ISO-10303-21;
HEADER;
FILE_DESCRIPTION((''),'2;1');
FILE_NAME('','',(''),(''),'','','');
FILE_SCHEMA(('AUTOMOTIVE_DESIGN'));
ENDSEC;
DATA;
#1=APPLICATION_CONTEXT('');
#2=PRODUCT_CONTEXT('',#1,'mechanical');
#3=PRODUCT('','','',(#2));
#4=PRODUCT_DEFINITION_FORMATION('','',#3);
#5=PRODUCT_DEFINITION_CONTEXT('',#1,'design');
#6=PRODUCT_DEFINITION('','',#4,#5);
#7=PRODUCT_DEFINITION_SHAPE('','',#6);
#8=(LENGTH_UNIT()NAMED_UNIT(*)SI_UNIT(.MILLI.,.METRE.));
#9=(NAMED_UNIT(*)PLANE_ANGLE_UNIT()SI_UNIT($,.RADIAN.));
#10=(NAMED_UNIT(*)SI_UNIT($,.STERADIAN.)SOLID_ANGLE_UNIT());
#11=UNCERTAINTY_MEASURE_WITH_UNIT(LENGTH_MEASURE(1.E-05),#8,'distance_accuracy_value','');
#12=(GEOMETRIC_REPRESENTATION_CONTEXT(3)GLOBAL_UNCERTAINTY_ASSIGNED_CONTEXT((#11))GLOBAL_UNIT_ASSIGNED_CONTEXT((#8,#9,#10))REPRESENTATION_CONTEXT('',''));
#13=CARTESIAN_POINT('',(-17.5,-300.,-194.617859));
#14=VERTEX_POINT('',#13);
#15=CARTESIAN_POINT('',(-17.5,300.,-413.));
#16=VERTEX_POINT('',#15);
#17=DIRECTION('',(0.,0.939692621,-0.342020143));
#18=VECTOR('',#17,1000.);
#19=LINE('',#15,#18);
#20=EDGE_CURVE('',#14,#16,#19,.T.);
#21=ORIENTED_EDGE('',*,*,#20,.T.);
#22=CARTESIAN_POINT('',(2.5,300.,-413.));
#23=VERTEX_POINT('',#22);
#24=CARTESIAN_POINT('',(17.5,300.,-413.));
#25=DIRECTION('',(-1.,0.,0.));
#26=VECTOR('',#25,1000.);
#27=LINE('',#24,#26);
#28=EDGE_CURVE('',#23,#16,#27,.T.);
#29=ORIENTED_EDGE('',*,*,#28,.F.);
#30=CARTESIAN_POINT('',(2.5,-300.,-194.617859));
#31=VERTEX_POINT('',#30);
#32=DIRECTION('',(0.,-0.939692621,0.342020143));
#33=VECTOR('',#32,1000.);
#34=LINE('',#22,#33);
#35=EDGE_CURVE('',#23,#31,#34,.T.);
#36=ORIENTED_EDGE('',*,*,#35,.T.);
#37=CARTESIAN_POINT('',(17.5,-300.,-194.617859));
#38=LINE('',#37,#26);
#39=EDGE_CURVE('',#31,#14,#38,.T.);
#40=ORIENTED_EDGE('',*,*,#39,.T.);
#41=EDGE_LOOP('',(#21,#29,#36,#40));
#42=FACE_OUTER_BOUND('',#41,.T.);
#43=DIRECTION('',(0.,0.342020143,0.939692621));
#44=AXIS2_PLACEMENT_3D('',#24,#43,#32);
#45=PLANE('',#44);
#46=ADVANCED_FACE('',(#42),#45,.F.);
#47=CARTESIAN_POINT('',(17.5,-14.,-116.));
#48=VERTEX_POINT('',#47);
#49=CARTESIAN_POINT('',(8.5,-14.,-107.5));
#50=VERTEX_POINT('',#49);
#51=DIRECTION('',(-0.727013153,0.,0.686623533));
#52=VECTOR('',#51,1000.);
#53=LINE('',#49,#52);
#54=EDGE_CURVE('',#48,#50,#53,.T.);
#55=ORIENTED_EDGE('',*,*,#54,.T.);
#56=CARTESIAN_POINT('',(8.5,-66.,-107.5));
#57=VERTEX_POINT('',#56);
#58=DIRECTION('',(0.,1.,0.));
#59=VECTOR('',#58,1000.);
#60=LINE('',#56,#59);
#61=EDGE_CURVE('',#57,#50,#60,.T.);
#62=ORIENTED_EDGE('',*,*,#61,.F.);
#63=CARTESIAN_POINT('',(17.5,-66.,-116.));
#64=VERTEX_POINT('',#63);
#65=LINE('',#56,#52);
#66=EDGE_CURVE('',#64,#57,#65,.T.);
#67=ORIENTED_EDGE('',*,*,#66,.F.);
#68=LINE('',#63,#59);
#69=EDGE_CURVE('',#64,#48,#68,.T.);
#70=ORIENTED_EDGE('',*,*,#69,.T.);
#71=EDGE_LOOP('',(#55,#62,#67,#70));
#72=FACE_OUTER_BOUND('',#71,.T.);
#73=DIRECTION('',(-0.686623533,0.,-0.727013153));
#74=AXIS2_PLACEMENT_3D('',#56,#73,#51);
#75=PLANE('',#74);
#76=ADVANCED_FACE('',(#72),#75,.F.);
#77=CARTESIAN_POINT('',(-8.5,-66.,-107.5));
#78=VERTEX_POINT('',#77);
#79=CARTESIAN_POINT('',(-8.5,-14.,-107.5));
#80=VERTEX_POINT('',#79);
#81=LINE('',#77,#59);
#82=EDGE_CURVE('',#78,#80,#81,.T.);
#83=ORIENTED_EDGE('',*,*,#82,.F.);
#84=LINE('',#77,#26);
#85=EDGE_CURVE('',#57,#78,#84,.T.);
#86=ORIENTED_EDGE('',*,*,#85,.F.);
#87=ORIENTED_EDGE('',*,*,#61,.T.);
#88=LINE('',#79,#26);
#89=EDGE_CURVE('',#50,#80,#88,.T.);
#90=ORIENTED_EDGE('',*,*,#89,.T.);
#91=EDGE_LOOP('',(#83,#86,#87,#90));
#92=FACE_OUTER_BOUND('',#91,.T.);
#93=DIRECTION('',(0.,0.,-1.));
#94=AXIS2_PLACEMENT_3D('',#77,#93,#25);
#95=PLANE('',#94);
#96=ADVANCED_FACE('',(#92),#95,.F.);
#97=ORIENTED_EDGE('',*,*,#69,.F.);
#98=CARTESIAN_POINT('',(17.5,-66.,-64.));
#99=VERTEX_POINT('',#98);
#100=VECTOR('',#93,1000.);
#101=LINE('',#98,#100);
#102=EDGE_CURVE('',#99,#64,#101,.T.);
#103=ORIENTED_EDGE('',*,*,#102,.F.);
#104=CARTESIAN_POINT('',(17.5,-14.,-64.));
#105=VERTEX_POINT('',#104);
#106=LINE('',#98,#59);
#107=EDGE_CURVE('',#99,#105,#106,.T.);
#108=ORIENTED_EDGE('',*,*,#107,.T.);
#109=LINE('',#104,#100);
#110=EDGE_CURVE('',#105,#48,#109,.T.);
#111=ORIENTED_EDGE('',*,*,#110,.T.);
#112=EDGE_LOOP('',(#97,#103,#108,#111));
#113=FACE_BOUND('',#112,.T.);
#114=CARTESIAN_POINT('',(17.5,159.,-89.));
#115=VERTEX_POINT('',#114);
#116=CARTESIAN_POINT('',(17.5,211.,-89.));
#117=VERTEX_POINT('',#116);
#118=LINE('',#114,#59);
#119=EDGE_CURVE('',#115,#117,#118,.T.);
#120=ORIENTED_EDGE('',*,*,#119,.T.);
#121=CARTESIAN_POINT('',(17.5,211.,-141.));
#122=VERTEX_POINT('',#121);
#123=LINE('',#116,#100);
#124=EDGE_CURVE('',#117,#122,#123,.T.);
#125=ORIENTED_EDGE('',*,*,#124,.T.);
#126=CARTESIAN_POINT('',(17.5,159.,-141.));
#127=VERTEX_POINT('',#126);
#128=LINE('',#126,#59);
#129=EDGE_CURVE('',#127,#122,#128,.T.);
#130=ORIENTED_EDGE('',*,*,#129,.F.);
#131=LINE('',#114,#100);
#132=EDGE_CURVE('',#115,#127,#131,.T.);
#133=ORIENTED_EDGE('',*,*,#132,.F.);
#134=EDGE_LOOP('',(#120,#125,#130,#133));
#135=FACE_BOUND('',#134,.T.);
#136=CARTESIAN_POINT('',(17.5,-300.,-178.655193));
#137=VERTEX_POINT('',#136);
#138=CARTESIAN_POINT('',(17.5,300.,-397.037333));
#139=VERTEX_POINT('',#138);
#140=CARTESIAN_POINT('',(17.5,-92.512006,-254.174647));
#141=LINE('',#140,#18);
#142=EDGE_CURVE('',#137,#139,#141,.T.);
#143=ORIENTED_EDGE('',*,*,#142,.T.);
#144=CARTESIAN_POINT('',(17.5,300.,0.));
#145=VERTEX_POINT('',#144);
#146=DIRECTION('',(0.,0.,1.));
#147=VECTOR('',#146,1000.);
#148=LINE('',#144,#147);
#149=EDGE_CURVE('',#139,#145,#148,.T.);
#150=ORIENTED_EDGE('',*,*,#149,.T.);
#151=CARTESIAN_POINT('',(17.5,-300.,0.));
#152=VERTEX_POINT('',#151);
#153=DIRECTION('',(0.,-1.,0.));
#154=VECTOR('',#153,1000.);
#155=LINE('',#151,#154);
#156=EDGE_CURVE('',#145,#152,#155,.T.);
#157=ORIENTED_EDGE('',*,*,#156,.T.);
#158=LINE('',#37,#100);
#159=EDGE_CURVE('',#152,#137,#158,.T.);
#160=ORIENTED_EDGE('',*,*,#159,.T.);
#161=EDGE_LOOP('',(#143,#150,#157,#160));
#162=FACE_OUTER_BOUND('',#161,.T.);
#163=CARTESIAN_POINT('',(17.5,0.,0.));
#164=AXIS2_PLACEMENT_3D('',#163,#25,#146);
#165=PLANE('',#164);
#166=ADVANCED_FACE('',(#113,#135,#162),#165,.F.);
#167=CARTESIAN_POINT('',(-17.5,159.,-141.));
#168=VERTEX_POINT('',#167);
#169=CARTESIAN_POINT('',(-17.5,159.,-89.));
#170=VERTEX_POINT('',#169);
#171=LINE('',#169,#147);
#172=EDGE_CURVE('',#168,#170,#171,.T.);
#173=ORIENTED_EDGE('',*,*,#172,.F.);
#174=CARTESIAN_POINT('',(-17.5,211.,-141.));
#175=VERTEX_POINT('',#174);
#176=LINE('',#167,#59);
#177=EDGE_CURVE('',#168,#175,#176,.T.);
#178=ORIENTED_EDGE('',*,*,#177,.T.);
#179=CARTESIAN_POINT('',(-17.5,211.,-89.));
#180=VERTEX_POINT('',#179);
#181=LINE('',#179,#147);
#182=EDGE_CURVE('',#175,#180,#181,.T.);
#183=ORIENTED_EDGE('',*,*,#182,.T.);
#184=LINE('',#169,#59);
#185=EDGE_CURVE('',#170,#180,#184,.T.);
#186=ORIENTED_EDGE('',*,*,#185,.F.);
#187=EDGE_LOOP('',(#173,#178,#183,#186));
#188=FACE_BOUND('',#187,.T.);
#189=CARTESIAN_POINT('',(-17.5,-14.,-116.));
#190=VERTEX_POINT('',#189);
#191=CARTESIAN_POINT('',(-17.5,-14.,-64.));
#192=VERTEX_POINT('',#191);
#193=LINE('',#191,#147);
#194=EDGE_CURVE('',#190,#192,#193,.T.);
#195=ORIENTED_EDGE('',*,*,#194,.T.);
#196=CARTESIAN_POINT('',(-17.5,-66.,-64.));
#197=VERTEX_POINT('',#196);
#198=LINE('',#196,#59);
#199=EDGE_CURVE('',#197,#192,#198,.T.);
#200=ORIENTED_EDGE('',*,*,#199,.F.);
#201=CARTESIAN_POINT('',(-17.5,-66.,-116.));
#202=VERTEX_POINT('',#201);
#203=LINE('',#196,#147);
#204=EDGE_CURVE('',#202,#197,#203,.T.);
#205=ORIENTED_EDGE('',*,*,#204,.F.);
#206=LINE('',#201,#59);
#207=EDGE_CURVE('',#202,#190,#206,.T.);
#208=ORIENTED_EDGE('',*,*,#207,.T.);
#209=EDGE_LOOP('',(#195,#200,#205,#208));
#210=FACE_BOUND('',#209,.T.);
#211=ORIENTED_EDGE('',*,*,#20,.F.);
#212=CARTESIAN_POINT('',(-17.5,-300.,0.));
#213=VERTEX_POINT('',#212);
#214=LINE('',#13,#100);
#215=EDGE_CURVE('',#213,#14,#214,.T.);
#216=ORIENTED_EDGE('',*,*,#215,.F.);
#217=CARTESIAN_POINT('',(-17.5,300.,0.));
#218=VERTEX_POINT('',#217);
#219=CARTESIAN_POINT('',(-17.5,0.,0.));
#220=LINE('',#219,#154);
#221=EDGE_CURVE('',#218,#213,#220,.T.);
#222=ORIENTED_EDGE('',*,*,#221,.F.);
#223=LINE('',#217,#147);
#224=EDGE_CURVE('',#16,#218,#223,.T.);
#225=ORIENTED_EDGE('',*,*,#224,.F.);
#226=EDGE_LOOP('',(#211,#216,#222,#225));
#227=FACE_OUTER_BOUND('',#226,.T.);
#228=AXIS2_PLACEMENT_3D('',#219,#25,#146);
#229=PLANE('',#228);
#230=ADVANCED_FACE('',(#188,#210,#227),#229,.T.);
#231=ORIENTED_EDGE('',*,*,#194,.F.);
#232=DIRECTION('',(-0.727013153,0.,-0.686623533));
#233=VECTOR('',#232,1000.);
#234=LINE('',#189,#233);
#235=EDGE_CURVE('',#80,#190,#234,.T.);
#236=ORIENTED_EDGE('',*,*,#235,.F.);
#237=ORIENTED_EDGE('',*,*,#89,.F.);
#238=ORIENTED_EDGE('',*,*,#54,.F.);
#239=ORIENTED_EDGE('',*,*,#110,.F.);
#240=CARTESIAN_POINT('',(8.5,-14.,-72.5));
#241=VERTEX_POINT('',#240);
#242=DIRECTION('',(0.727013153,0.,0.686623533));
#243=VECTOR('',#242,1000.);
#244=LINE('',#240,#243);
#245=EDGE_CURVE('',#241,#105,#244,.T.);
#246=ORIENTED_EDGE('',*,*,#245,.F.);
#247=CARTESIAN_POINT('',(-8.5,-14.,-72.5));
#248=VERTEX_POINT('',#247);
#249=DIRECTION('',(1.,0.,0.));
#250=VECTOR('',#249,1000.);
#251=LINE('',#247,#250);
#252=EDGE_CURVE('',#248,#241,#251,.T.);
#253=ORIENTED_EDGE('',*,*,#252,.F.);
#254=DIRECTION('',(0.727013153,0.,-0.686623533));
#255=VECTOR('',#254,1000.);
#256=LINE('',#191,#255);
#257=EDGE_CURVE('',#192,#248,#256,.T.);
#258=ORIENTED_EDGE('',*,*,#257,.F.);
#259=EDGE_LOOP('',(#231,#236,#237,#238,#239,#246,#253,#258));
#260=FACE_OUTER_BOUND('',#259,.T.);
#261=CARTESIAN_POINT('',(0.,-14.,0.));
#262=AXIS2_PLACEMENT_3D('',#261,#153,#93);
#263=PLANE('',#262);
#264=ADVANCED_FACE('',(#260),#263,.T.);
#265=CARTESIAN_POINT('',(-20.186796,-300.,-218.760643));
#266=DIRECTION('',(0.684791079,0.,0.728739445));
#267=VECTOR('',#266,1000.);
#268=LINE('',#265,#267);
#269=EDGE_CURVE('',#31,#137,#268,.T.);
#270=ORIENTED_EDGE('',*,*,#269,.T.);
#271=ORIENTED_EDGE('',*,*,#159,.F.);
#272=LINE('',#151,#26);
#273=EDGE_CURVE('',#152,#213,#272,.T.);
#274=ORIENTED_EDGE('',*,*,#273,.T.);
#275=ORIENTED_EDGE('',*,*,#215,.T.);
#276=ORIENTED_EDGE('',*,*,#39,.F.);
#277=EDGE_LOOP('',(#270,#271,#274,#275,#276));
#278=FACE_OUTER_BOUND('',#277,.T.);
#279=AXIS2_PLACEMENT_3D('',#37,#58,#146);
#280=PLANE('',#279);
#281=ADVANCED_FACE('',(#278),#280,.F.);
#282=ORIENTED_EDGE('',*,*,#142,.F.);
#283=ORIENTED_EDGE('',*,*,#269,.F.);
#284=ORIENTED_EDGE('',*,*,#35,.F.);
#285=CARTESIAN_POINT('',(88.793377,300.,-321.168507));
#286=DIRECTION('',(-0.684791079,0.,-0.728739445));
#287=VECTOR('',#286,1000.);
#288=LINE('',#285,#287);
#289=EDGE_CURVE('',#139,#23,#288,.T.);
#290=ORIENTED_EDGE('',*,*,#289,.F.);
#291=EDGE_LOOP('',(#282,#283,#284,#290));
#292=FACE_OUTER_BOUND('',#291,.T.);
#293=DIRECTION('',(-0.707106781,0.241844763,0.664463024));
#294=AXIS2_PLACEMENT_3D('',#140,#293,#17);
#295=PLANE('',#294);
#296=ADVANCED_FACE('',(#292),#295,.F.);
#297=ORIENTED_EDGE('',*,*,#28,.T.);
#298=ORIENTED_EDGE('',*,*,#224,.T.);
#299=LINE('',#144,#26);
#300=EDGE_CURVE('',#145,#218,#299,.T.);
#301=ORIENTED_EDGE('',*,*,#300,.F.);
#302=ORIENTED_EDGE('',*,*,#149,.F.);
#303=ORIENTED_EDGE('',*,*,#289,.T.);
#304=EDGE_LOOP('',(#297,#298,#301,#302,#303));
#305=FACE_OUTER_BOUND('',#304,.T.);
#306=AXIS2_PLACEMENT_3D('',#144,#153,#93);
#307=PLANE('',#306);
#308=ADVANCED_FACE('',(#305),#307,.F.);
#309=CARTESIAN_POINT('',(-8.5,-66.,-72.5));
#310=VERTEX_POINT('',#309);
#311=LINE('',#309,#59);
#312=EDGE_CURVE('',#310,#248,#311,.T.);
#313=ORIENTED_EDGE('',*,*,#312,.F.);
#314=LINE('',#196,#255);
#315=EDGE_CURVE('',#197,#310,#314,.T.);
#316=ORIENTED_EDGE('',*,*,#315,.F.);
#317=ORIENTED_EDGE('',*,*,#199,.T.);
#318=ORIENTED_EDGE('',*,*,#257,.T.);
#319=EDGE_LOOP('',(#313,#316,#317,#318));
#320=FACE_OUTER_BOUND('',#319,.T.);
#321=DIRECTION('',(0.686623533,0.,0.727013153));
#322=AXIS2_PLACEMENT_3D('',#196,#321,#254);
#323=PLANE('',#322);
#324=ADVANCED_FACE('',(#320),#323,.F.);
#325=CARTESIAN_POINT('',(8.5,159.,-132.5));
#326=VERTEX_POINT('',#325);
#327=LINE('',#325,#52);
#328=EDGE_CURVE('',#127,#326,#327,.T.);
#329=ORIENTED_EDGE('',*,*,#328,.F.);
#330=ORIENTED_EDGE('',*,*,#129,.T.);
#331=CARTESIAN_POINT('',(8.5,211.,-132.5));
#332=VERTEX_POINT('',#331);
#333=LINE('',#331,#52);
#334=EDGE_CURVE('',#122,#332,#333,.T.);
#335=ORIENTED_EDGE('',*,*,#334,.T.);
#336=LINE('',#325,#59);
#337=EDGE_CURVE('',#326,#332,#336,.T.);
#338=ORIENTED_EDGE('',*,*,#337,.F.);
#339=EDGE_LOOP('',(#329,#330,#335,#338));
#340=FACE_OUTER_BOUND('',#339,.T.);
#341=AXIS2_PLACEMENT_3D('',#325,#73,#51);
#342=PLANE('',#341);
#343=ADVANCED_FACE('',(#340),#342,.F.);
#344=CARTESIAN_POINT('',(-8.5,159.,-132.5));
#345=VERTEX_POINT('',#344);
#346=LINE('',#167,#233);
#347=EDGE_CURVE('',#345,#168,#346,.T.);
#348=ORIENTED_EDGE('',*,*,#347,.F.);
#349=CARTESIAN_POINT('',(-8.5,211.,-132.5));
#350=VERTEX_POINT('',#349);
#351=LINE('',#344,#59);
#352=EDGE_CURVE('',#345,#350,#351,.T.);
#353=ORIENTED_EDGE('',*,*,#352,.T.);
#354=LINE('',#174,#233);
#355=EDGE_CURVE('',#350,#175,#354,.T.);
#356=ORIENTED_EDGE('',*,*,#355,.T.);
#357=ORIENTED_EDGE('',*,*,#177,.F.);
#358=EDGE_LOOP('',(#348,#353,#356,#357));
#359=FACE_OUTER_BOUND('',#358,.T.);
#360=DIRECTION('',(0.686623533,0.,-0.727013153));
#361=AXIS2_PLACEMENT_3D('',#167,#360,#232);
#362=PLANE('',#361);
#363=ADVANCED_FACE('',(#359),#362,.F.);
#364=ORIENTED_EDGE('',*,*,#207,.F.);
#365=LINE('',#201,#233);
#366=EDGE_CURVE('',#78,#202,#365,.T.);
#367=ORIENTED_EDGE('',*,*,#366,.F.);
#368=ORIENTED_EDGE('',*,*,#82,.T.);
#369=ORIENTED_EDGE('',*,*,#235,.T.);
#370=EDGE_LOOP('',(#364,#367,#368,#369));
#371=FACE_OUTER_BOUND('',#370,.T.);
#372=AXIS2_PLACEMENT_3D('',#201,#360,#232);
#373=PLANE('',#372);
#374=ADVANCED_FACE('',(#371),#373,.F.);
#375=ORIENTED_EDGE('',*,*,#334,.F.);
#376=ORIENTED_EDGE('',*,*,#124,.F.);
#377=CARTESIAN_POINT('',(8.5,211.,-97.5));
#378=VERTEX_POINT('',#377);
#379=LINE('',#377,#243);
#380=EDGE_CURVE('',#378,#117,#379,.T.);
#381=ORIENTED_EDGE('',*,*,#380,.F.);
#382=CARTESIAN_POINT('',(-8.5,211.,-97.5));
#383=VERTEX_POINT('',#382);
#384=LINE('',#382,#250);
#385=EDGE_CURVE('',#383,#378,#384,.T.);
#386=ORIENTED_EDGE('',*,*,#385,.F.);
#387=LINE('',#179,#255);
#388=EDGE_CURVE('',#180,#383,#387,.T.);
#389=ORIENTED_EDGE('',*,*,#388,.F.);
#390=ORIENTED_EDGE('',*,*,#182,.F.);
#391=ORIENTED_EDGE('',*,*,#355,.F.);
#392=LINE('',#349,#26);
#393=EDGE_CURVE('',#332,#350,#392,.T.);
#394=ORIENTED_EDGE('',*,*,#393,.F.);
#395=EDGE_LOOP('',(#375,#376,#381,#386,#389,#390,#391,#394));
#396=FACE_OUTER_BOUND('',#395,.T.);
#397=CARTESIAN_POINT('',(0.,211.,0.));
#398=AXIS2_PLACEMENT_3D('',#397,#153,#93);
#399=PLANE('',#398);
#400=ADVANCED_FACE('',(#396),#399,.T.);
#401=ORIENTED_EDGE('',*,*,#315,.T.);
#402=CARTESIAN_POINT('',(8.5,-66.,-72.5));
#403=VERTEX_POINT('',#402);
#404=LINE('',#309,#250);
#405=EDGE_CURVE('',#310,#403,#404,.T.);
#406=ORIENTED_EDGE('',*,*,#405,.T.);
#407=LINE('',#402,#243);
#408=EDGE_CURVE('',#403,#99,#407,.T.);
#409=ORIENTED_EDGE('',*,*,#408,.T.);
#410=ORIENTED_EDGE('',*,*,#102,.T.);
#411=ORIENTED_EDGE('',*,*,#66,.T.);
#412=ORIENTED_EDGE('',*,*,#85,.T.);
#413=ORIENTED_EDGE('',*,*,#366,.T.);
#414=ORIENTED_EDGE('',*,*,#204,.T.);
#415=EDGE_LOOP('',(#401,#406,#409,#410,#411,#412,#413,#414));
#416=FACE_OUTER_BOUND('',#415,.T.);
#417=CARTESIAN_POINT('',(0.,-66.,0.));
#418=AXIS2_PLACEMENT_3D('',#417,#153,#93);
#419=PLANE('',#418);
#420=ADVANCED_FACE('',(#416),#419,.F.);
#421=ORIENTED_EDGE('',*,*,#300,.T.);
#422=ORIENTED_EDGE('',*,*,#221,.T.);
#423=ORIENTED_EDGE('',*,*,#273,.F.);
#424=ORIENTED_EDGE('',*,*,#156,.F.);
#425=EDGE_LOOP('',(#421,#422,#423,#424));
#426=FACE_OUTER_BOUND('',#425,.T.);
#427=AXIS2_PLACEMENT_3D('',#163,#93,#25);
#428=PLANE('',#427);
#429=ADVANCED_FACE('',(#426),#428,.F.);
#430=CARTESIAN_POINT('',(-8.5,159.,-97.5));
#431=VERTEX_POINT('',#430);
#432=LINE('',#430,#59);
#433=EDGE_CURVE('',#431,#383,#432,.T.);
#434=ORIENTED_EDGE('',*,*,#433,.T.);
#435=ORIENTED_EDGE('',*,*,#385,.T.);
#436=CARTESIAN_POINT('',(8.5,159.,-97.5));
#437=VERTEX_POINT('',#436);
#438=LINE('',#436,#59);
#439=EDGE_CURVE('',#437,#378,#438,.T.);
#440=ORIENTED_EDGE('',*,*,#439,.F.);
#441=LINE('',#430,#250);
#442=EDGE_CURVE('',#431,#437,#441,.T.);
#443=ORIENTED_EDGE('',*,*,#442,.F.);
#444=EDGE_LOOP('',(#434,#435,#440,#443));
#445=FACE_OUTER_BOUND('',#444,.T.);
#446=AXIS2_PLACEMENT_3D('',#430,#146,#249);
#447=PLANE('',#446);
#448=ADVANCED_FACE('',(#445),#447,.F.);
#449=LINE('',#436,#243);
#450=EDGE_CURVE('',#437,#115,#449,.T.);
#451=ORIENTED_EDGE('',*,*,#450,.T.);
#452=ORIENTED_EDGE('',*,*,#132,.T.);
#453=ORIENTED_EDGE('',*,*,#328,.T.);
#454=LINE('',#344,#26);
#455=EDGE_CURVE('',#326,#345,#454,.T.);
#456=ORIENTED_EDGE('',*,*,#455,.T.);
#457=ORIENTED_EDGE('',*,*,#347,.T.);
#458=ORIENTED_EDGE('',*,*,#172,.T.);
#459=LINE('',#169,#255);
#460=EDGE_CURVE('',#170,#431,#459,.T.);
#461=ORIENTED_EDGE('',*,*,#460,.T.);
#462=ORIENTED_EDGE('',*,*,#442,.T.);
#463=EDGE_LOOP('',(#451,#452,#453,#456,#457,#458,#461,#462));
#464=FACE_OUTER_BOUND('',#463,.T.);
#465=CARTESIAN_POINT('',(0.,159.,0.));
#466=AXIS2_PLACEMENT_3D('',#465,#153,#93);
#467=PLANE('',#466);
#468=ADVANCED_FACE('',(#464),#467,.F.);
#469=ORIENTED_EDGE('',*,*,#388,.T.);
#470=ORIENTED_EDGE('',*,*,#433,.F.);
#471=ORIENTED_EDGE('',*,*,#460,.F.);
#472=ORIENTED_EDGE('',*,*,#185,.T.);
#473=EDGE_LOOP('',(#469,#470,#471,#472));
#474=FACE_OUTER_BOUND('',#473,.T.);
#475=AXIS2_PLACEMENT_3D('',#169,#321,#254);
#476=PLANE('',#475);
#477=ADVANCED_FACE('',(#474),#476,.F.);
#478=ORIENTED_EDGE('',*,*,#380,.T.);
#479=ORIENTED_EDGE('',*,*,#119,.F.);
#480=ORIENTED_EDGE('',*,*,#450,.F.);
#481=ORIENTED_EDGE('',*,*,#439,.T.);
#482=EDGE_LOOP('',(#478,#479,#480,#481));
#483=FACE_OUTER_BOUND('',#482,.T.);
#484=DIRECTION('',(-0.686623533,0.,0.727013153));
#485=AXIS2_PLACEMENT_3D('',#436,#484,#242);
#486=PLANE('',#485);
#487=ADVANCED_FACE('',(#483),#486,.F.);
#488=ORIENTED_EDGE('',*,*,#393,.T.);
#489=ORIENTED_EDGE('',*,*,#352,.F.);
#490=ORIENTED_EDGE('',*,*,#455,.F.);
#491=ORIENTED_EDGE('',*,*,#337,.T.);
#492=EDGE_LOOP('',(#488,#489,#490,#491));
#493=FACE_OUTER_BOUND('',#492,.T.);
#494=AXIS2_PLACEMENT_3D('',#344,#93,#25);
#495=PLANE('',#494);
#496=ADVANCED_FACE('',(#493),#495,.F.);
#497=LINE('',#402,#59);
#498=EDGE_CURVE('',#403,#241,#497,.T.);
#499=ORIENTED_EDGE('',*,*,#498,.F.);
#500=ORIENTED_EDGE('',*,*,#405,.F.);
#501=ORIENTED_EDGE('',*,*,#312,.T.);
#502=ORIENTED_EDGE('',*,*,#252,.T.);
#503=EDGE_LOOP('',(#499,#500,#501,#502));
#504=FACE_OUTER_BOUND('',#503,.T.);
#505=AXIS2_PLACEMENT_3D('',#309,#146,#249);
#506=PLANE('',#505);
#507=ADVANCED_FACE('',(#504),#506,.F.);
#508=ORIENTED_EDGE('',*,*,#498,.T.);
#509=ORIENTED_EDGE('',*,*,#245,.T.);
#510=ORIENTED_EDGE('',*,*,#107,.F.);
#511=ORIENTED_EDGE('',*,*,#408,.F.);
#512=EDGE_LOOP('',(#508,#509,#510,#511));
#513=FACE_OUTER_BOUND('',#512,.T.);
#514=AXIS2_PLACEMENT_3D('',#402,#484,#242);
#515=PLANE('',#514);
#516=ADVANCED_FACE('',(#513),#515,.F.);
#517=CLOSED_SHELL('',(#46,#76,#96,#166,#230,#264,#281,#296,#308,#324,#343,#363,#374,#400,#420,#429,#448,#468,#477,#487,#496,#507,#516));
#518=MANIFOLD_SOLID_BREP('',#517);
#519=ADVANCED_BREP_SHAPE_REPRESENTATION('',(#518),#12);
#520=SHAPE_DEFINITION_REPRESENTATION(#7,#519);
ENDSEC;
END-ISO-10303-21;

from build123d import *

# Parameters (mm, degrees)
BOSS_EXTRUDE1_DEPTH = 17.5
CUT_EXTRUDE1_START  = 185
CUT_EXTRUDE1_DEPTH  = 26
CHAMFER2_SIZE       = 15
CUT_EXTRUDE2_START  = -40
CUT_EXTRUDE2_DEPTH  = 26


with BuildPart() as part:
    # Sketch1 → Boss-Extrude1 (new, symmetric)
    with BuildSketch(Plane(origin=(0, 0, 0), x_dir=(0, 0, -1), z_dir=(1, 0, 0))):
        Polygon((0, 0), (0, 300), (413, 300), (194.61785944, -300), (0, -300), align=None)
    extrude(amount=BOSS_EXTRUDE1_DEPTH, both=True)

    # Sketch2 → Cut-Extrude1 (cut, symmetric)
    with BuildSketch(Plane(origin=(0, 0, 0), x_dir=(1, 0, 0), z_dir=(0, 1, 0)).offset(CUT_EXTRUDE1_START)):
        Polygon((-17.5, 89), (-8.5, 97.5), (8.5, 97.5), (17.5, 89), (17.5, 141), (8.5, 132.5), (-8.5, 132.5), (-17.5, 141), align=None)
    extrude(amount=CUT_EXTRUDE1_DEPTH, both=True, mode=Mode.SUBTRACT)

    # Chamfer2
    chamfer2_edges = [part.edges().sort_by_distance(p)[0] for p in [
        (17.5, 0, -303.80892972),
    ]]
    chamfer(chamfer2_edges, length=CHAMFER2_SIZE)

    # Sketch3 → Cut-Extrude2 (cut, symmetric)
    with BuildSketch(Plane(origin=(0, 0, 0), x_dir=(1, 0, 0), z_dir=(0, 1, 0)).offset(CUT_EXTRUDE2_START)):
        Polygon((-17.5, 64), (-8.5, 72.5), (8.5, 72.5), (17.5, 64), (17.5, 116), (8.5, 107.5), (-8.5, 107.5), (-17.5, 116), align=None)
    extrude(amount=CUT_EXTRUDE2_DEPTH, both=True, mode=Mode.SUBTRACT)


solid = part.part
